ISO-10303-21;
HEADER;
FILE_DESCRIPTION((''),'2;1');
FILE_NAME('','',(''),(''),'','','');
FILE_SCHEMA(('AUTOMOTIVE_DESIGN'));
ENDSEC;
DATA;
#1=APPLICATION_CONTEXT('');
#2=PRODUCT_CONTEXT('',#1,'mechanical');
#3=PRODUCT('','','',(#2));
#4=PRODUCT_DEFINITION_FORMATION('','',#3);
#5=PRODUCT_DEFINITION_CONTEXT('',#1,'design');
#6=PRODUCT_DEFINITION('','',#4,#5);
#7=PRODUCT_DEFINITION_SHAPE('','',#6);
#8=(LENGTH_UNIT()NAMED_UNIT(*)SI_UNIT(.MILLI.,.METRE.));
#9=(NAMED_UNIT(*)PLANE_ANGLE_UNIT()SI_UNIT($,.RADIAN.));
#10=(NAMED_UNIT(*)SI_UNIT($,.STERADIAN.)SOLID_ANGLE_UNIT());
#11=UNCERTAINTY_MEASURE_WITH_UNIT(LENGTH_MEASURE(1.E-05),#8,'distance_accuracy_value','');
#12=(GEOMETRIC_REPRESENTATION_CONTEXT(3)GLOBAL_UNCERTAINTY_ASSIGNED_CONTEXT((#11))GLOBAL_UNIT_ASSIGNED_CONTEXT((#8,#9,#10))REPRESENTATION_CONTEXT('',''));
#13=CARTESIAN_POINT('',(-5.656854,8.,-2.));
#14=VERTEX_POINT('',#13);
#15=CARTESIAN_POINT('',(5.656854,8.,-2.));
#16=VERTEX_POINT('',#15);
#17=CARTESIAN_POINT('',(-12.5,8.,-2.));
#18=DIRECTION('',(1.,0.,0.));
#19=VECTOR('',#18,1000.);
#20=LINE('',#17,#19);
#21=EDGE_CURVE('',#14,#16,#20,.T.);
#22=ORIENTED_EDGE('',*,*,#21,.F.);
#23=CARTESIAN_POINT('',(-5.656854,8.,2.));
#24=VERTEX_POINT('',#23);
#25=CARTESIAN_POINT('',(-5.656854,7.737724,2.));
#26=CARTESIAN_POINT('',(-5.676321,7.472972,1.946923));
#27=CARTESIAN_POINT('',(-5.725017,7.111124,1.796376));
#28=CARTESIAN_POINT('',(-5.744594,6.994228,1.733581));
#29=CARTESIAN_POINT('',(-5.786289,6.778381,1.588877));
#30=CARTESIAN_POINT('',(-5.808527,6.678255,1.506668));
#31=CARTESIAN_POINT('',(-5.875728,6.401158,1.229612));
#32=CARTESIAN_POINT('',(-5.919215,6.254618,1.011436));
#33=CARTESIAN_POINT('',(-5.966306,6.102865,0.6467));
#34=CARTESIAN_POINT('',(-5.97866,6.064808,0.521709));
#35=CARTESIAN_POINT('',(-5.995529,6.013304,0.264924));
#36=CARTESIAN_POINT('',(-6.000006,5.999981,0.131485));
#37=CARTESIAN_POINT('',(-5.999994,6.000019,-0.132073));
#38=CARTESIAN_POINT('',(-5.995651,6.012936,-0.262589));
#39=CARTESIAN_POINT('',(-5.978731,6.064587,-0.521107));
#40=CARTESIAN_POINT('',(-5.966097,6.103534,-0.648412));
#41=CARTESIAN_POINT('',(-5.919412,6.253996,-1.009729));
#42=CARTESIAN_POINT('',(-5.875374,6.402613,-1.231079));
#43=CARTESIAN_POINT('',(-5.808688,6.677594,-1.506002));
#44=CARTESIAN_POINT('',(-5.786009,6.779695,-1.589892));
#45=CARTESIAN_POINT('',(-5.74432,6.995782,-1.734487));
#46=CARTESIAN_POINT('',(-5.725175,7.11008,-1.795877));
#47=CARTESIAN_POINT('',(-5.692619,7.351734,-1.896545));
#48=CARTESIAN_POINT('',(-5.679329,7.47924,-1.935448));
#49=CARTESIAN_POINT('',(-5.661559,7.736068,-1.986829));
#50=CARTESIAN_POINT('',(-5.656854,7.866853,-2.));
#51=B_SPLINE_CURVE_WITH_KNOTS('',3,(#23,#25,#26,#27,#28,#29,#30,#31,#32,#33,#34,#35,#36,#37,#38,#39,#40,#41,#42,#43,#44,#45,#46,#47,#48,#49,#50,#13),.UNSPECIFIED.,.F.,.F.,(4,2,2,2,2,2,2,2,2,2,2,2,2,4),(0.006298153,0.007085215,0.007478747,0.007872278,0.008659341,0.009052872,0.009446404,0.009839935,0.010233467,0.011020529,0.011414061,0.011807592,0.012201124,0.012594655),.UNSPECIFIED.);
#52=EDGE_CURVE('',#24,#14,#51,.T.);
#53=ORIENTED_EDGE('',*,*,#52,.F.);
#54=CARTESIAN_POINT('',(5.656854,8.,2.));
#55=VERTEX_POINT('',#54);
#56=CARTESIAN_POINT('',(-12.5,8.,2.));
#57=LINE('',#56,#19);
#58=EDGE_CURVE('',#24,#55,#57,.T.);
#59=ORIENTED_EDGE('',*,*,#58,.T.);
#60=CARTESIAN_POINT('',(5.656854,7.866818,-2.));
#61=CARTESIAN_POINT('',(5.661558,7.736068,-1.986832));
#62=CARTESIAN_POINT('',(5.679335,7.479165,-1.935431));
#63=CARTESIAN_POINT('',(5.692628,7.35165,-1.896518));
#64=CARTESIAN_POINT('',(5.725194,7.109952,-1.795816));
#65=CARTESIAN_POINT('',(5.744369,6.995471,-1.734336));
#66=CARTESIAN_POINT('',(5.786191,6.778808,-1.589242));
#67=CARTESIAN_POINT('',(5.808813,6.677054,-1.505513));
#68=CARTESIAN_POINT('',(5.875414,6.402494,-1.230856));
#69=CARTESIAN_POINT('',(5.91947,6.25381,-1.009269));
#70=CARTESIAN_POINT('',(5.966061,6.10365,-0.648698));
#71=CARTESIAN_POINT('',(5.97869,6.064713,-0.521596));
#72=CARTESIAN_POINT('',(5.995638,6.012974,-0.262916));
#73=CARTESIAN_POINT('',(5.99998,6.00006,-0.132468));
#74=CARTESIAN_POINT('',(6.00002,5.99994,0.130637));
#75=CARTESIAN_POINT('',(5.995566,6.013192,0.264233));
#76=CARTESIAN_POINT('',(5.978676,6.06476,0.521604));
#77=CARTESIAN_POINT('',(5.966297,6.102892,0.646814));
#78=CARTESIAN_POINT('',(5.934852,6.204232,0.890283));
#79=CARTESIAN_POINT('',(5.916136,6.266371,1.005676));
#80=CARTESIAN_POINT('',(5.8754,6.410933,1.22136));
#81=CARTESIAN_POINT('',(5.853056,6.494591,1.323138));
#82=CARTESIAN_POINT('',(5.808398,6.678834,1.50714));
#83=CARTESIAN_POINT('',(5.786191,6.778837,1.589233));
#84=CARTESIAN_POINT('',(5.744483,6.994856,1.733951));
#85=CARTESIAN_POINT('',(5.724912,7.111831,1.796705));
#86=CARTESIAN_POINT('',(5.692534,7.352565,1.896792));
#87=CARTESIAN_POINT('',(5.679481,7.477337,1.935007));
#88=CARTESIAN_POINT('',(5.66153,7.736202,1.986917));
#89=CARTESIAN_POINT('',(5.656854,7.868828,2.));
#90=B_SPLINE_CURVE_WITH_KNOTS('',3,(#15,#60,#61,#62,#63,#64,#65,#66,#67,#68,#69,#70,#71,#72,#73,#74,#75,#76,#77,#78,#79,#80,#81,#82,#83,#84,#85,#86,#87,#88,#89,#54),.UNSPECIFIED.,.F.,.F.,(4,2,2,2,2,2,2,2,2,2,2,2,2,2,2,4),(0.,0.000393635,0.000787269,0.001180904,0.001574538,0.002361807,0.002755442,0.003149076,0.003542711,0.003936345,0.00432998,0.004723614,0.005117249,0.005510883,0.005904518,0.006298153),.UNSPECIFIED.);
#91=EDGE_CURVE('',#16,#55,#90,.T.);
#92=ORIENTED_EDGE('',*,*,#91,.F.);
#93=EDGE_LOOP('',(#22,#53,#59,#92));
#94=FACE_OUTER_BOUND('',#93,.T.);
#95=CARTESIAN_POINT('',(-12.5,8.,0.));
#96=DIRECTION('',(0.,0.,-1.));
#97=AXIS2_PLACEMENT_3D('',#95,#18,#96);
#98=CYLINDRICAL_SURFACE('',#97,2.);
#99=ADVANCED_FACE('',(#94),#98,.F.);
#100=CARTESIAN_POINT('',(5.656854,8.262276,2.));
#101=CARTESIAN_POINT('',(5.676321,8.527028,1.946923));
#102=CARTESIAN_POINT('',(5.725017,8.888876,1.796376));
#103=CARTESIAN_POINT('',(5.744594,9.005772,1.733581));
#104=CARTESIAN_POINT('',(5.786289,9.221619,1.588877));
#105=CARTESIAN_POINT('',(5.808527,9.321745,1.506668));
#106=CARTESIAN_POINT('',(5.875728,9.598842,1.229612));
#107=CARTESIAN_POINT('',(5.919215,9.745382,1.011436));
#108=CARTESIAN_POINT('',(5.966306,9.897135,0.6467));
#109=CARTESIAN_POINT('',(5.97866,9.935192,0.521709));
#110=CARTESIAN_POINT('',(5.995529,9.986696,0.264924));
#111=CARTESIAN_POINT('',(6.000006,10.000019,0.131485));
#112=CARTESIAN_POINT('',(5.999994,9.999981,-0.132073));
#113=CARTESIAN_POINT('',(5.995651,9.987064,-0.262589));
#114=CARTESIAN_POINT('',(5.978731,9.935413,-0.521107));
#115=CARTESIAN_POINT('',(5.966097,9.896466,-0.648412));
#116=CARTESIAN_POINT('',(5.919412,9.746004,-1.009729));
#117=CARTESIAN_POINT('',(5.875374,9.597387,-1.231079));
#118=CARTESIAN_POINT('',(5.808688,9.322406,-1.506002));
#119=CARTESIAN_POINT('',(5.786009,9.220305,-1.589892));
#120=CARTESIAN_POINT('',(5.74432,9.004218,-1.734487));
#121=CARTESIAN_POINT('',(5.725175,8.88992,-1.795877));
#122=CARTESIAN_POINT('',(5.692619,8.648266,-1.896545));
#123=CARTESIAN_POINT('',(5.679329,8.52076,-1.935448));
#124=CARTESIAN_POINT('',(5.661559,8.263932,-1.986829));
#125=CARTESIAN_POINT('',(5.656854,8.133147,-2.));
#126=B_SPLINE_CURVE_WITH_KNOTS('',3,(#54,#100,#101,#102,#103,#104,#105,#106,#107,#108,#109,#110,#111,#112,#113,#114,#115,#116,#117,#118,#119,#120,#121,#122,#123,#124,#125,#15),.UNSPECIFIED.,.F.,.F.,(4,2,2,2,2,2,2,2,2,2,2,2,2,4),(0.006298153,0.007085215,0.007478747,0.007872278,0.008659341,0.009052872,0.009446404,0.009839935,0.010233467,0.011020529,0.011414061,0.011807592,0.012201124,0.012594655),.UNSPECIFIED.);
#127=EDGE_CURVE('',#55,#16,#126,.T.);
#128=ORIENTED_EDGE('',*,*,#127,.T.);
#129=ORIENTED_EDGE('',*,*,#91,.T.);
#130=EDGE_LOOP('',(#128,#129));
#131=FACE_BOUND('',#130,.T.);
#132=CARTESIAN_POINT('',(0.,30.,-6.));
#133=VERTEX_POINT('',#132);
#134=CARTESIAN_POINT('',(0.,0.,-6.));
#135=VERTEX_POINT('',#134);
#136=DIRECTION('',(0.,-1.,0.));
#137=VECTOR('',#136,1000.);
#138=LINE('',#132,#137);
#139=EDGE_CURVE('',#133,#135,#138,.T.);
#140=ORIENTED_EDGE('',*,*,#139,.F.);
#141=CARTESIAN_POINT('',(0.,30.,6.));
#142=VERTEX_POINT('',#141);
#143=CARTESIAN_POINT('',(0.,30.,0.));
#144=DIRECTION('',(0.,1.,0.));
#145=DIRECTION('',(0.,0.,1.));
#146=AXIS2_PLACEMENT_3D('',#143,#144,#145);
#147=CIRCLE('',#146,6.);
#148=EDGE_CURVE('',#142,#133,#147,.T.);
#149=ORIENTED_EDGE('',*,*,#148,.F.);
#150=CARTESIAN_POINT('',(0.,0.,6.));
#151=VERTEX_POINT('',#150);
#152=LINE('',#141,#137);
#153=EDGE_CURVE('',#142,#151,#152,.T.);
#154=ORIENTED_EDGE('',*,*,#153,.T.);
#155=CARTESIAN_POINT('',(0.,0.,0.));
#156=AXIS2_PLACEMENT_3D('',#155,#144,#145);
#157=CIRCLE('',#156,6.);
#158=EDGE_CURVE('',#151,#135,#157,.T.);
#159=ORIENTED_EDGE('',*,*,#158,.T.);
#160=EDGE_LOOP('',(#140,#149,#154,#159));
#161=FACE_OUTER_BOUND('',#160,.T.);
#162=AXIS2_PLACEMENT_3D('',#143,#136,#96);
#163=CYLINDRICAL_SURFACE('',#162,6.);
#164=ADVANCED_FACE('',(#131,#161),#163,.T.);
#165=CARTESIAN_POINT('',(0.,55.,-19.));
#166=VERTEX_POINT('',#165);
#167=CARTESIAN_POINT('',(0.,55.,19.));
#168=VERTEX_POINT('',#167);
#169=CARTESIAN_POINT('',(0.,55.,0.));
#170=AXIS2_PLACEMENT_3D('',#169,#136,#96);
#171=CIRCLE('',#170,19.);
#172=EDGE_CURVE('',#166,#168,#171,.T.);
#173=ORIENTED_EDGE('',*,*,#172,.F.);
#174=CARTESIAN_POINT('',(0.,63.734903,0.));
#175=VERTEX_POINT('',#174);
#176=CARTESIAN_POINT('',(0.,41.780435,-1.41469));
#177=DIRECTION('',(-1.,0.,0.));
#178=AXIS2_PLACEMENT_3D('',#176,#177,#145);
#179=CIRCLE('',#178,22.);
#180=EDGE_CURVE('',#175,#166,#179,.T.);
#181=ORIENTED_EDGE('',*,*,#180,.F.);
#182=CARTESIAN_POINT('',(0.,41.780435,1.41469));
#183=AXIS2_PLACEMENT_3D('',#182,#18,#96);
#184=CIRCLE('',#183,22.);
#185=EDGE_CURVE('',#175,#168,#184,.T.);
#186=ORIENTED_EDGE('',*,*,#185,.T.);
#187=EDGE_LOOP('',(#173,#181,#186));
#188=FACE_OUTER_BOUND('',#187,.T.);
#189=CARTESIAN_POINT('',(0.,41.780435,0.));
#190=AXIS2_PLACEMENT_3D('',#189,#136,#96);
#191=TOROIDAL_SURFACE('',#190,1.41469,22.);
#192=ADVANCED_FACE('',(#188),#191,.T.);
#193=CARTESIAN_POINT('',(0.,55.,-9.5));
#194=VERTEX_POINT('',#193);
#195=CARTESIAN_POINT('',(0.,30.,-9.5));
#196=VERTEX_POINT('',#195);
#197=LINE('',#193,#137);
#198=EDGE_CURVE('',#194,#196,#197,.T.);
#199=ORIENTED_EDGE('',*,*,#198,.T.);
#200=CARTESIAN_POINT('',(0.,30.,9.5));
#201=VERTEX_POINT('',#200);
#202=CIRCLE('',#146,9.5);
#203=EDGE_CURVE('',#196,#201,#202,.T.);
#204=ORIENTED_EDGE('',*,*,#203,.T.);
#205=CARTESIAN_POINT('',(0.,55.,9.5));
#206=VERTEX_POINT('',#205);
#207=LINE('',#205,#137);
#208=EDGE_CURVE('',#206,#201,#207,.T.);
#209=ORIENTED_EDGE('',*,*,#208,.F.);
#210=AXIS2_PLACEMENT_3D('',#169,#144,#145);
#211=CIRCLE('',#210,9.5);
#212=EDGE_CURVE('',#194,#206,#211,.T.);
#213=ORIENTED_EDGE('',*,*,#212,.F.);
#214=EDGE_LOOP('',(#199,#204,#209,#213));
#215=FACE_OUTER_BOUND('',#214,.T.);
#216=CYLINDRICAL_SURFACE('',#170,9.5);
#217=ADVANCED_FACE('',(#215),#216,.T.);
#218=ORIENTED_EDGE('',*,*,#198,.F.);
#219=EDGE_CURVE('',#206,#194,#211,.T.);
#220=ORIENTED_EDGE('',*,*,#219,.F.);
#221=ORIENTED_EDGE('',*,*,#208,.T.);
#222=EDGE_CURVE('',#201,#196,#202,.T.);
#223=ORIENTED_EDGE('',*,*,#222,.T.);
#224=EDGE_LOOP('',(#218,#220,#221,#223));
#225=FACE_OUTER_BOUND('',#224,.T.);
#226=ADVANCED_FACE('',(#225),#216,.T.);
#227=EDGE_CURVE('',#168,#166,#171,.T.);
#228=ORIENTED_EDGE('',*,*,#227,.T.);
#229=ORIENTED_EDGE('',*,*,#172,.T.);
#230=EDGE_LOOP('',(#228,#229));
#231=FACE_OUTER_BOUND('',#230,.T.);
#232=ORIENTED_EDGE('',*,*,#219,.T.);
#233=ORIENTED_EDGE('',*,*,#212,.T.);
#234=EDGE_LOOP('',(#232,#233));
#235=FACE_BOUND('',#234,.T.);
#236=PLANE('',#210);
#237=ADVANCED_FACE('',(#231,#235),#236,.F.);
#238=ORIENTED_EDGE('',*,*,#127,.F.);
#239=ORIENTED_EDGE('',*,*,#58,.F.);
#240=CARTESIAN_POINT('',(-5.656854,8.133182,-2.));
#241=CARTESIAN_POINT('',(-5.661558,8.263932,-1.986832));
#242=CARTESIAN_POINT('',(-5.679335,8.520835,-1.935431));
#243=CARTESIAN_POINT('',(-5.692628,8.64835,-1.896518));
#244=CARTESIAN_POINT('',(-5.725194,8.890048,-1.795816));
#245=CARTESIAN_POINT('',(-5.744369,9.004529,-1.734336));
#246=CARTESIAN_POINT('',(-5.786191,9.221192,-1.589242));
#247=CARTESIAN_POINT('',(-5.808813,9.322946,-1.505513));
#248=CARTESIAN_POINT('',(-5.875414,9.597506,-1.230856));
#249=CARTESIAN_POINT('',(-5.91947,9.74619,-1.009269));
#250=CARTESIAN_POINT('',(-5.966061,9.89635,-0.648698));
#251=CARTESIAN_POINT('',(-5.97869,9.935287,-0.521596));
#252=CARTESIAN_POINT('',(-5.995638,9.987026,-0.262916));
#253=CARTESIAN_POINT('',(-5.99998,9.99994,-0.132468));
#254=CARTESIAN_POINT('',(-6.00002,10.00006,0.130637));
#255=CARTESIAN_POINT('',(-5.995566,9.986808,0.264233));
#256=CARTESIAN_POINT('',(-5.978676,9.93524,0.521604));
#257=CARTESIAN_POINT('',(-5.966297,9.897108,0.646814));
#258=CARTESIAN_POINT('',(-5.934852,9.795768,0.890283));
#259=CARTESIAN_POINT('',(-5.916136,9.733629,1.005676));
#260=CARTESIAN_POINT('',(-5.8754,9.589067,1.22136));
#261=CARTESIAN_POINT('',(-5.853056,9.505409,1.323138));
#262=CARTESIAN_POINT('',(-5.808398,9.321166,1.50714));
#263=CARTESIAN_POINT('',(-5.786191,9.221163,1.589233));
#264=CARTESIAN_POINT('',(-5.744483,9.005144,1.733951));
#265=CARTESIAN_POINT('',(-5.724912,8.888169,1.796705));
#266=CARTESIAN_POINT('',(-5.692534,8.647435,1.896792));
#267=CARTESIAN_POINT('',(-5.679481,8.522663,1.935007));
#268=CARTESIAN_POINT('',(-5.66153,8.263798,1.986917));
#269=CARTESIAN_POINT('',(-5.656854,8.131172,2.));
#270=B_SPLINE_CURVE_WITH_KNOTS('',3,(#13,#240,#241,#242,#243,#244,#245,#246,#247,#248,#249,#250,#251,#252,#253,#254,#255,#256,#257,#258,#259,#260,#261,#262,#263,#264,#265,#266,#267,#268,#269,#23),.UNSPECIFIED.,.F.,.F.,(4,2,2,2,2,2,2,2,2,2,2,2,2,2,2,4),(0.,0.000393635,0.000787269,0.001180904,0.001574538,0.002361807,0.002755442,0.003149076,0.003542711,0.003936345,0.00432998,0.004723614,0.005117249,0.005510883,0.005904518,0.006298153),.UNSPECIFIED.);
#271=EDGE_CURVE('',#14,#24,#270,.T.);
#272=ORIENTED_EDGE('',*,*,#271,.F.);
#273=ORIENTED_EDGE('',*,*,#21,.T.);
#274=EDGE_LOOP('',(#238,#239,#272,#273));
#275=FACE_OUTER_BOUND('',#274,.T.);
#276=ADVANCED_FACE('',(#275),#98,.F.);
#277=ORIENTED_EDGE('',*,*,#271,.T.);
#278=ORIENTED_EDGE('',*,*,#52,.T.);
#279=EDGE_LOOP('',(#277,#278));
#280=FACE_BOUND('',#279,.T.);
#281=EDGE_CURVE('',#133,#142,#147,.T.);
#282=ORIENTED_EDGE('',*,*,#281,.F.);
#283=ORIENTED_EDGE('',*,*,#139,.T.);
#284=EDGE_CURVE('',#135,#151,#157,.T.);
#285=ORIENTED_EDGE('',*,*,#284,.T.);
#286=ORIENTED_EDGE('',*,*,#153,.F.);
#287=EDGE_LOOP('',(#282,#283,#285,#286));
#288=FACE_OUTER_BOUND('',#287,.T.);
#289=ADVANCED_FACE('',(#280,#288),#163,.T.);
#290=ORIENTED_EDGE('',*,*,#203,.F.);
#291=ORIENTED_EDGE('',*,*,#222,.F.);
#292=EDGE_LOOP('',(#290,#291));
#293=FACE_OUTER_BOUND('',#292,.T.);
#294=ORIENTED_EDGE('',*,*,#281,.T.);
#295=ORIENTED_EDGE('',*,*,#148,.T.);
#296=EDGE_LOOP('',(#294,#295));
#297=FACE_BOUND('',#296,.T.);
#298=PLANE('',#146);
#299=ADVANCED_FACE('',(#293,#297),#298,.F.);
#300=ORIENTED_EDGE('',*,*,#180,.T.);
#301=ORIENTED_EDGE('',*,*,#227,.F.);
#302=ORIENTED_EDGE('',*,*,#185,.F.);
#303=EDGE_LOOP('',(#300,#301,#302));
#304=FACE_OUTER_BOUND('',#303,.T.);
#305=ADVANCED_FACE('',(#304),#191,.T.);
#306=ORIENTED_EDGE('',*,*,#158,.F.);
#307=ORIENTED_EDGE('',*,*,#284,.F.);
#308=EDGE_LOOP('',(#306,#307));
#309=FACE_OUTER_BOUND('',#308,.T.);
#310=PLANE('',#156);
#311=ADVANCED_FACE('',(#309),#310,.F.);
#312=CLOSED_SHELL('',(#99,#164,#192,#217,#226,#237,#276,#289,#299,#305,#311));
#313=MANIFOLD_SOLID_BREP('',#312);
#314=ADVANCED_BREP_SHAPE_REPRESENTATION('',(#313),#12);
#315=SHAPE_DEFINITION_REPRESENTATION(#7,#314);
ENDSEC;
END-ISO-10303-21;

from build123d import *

# Parameters (mm, degrees)
SHAFT_PROFILE_12_R   = 6
SHAFT_12_DEPTH       = 30
COLLAR_PROFILE_19_R  = 9.5
COLLAR_19_DEPTH      = 25
CROSS_HOLE_PROFILE_R = 2
CROSS_HOLE_DEPTH     = 12.5


with BuildPart() as part:
    # Shaft Profile Ø12 → Shaft Ø12 (new body)
    with BuildSketch(Plane(origin=(0, 0, 0), x_dir=(1, 0, 0), z_dir=(0, 1, 0))):
        with Locations(Location((0, 0, 0), (0, 0, 270))):
            Circle(SHAFT_PROFILE_12_R)
    extrude(amount=SHAFT_12_DEPTH)

    # Collar Profile Ø19 → Collar Ø19 (add)
    with BuildSketch(Plane(origin=(0, 30, 0), x_dir=(1, 0, 0), z_dir=(0, 1, 0))):
        with Locations(Location((0, 0, 0), (0, 0, 270))):
            Circle(COLLAR_PROFILE_19_R)
    extrude(amount=COLLAR_19_DEPTH)

    # Dome Head Profile → Dome Head (revolve)
    with BuildSketch(Plane(origin=(0, 0, 0), x_dir=(0, 0, -1), z_dir=(1, 0, 0))):
        with BuildLine():
            Line((0, 55), (-19, 55))
            ThreePointArc((-19, 55), (-10.604187915, 61.769260733), (0, 63.734903146))
            Line((0, 63.734903146), (0, 55))
        make_face()
    revolve(axis=Axis((0, 55, 0), (0, 1, 0)))

    # Cross Hole Profile → Cross Hole (cut, symmetric)
    with BuildSketch(Plane(origin=(0, 0, 0), x_dir=(0, 0, -1), z_dir=(1, 0, 0))):
        with Locations((0, 8)):
            Circle(CROSS_HOLE_PROFILE_R)
    extrude(amount=CROSS_HOLE_DEPTH, both=True, mode=Mode.SUBTRACT)


solid = part.part
